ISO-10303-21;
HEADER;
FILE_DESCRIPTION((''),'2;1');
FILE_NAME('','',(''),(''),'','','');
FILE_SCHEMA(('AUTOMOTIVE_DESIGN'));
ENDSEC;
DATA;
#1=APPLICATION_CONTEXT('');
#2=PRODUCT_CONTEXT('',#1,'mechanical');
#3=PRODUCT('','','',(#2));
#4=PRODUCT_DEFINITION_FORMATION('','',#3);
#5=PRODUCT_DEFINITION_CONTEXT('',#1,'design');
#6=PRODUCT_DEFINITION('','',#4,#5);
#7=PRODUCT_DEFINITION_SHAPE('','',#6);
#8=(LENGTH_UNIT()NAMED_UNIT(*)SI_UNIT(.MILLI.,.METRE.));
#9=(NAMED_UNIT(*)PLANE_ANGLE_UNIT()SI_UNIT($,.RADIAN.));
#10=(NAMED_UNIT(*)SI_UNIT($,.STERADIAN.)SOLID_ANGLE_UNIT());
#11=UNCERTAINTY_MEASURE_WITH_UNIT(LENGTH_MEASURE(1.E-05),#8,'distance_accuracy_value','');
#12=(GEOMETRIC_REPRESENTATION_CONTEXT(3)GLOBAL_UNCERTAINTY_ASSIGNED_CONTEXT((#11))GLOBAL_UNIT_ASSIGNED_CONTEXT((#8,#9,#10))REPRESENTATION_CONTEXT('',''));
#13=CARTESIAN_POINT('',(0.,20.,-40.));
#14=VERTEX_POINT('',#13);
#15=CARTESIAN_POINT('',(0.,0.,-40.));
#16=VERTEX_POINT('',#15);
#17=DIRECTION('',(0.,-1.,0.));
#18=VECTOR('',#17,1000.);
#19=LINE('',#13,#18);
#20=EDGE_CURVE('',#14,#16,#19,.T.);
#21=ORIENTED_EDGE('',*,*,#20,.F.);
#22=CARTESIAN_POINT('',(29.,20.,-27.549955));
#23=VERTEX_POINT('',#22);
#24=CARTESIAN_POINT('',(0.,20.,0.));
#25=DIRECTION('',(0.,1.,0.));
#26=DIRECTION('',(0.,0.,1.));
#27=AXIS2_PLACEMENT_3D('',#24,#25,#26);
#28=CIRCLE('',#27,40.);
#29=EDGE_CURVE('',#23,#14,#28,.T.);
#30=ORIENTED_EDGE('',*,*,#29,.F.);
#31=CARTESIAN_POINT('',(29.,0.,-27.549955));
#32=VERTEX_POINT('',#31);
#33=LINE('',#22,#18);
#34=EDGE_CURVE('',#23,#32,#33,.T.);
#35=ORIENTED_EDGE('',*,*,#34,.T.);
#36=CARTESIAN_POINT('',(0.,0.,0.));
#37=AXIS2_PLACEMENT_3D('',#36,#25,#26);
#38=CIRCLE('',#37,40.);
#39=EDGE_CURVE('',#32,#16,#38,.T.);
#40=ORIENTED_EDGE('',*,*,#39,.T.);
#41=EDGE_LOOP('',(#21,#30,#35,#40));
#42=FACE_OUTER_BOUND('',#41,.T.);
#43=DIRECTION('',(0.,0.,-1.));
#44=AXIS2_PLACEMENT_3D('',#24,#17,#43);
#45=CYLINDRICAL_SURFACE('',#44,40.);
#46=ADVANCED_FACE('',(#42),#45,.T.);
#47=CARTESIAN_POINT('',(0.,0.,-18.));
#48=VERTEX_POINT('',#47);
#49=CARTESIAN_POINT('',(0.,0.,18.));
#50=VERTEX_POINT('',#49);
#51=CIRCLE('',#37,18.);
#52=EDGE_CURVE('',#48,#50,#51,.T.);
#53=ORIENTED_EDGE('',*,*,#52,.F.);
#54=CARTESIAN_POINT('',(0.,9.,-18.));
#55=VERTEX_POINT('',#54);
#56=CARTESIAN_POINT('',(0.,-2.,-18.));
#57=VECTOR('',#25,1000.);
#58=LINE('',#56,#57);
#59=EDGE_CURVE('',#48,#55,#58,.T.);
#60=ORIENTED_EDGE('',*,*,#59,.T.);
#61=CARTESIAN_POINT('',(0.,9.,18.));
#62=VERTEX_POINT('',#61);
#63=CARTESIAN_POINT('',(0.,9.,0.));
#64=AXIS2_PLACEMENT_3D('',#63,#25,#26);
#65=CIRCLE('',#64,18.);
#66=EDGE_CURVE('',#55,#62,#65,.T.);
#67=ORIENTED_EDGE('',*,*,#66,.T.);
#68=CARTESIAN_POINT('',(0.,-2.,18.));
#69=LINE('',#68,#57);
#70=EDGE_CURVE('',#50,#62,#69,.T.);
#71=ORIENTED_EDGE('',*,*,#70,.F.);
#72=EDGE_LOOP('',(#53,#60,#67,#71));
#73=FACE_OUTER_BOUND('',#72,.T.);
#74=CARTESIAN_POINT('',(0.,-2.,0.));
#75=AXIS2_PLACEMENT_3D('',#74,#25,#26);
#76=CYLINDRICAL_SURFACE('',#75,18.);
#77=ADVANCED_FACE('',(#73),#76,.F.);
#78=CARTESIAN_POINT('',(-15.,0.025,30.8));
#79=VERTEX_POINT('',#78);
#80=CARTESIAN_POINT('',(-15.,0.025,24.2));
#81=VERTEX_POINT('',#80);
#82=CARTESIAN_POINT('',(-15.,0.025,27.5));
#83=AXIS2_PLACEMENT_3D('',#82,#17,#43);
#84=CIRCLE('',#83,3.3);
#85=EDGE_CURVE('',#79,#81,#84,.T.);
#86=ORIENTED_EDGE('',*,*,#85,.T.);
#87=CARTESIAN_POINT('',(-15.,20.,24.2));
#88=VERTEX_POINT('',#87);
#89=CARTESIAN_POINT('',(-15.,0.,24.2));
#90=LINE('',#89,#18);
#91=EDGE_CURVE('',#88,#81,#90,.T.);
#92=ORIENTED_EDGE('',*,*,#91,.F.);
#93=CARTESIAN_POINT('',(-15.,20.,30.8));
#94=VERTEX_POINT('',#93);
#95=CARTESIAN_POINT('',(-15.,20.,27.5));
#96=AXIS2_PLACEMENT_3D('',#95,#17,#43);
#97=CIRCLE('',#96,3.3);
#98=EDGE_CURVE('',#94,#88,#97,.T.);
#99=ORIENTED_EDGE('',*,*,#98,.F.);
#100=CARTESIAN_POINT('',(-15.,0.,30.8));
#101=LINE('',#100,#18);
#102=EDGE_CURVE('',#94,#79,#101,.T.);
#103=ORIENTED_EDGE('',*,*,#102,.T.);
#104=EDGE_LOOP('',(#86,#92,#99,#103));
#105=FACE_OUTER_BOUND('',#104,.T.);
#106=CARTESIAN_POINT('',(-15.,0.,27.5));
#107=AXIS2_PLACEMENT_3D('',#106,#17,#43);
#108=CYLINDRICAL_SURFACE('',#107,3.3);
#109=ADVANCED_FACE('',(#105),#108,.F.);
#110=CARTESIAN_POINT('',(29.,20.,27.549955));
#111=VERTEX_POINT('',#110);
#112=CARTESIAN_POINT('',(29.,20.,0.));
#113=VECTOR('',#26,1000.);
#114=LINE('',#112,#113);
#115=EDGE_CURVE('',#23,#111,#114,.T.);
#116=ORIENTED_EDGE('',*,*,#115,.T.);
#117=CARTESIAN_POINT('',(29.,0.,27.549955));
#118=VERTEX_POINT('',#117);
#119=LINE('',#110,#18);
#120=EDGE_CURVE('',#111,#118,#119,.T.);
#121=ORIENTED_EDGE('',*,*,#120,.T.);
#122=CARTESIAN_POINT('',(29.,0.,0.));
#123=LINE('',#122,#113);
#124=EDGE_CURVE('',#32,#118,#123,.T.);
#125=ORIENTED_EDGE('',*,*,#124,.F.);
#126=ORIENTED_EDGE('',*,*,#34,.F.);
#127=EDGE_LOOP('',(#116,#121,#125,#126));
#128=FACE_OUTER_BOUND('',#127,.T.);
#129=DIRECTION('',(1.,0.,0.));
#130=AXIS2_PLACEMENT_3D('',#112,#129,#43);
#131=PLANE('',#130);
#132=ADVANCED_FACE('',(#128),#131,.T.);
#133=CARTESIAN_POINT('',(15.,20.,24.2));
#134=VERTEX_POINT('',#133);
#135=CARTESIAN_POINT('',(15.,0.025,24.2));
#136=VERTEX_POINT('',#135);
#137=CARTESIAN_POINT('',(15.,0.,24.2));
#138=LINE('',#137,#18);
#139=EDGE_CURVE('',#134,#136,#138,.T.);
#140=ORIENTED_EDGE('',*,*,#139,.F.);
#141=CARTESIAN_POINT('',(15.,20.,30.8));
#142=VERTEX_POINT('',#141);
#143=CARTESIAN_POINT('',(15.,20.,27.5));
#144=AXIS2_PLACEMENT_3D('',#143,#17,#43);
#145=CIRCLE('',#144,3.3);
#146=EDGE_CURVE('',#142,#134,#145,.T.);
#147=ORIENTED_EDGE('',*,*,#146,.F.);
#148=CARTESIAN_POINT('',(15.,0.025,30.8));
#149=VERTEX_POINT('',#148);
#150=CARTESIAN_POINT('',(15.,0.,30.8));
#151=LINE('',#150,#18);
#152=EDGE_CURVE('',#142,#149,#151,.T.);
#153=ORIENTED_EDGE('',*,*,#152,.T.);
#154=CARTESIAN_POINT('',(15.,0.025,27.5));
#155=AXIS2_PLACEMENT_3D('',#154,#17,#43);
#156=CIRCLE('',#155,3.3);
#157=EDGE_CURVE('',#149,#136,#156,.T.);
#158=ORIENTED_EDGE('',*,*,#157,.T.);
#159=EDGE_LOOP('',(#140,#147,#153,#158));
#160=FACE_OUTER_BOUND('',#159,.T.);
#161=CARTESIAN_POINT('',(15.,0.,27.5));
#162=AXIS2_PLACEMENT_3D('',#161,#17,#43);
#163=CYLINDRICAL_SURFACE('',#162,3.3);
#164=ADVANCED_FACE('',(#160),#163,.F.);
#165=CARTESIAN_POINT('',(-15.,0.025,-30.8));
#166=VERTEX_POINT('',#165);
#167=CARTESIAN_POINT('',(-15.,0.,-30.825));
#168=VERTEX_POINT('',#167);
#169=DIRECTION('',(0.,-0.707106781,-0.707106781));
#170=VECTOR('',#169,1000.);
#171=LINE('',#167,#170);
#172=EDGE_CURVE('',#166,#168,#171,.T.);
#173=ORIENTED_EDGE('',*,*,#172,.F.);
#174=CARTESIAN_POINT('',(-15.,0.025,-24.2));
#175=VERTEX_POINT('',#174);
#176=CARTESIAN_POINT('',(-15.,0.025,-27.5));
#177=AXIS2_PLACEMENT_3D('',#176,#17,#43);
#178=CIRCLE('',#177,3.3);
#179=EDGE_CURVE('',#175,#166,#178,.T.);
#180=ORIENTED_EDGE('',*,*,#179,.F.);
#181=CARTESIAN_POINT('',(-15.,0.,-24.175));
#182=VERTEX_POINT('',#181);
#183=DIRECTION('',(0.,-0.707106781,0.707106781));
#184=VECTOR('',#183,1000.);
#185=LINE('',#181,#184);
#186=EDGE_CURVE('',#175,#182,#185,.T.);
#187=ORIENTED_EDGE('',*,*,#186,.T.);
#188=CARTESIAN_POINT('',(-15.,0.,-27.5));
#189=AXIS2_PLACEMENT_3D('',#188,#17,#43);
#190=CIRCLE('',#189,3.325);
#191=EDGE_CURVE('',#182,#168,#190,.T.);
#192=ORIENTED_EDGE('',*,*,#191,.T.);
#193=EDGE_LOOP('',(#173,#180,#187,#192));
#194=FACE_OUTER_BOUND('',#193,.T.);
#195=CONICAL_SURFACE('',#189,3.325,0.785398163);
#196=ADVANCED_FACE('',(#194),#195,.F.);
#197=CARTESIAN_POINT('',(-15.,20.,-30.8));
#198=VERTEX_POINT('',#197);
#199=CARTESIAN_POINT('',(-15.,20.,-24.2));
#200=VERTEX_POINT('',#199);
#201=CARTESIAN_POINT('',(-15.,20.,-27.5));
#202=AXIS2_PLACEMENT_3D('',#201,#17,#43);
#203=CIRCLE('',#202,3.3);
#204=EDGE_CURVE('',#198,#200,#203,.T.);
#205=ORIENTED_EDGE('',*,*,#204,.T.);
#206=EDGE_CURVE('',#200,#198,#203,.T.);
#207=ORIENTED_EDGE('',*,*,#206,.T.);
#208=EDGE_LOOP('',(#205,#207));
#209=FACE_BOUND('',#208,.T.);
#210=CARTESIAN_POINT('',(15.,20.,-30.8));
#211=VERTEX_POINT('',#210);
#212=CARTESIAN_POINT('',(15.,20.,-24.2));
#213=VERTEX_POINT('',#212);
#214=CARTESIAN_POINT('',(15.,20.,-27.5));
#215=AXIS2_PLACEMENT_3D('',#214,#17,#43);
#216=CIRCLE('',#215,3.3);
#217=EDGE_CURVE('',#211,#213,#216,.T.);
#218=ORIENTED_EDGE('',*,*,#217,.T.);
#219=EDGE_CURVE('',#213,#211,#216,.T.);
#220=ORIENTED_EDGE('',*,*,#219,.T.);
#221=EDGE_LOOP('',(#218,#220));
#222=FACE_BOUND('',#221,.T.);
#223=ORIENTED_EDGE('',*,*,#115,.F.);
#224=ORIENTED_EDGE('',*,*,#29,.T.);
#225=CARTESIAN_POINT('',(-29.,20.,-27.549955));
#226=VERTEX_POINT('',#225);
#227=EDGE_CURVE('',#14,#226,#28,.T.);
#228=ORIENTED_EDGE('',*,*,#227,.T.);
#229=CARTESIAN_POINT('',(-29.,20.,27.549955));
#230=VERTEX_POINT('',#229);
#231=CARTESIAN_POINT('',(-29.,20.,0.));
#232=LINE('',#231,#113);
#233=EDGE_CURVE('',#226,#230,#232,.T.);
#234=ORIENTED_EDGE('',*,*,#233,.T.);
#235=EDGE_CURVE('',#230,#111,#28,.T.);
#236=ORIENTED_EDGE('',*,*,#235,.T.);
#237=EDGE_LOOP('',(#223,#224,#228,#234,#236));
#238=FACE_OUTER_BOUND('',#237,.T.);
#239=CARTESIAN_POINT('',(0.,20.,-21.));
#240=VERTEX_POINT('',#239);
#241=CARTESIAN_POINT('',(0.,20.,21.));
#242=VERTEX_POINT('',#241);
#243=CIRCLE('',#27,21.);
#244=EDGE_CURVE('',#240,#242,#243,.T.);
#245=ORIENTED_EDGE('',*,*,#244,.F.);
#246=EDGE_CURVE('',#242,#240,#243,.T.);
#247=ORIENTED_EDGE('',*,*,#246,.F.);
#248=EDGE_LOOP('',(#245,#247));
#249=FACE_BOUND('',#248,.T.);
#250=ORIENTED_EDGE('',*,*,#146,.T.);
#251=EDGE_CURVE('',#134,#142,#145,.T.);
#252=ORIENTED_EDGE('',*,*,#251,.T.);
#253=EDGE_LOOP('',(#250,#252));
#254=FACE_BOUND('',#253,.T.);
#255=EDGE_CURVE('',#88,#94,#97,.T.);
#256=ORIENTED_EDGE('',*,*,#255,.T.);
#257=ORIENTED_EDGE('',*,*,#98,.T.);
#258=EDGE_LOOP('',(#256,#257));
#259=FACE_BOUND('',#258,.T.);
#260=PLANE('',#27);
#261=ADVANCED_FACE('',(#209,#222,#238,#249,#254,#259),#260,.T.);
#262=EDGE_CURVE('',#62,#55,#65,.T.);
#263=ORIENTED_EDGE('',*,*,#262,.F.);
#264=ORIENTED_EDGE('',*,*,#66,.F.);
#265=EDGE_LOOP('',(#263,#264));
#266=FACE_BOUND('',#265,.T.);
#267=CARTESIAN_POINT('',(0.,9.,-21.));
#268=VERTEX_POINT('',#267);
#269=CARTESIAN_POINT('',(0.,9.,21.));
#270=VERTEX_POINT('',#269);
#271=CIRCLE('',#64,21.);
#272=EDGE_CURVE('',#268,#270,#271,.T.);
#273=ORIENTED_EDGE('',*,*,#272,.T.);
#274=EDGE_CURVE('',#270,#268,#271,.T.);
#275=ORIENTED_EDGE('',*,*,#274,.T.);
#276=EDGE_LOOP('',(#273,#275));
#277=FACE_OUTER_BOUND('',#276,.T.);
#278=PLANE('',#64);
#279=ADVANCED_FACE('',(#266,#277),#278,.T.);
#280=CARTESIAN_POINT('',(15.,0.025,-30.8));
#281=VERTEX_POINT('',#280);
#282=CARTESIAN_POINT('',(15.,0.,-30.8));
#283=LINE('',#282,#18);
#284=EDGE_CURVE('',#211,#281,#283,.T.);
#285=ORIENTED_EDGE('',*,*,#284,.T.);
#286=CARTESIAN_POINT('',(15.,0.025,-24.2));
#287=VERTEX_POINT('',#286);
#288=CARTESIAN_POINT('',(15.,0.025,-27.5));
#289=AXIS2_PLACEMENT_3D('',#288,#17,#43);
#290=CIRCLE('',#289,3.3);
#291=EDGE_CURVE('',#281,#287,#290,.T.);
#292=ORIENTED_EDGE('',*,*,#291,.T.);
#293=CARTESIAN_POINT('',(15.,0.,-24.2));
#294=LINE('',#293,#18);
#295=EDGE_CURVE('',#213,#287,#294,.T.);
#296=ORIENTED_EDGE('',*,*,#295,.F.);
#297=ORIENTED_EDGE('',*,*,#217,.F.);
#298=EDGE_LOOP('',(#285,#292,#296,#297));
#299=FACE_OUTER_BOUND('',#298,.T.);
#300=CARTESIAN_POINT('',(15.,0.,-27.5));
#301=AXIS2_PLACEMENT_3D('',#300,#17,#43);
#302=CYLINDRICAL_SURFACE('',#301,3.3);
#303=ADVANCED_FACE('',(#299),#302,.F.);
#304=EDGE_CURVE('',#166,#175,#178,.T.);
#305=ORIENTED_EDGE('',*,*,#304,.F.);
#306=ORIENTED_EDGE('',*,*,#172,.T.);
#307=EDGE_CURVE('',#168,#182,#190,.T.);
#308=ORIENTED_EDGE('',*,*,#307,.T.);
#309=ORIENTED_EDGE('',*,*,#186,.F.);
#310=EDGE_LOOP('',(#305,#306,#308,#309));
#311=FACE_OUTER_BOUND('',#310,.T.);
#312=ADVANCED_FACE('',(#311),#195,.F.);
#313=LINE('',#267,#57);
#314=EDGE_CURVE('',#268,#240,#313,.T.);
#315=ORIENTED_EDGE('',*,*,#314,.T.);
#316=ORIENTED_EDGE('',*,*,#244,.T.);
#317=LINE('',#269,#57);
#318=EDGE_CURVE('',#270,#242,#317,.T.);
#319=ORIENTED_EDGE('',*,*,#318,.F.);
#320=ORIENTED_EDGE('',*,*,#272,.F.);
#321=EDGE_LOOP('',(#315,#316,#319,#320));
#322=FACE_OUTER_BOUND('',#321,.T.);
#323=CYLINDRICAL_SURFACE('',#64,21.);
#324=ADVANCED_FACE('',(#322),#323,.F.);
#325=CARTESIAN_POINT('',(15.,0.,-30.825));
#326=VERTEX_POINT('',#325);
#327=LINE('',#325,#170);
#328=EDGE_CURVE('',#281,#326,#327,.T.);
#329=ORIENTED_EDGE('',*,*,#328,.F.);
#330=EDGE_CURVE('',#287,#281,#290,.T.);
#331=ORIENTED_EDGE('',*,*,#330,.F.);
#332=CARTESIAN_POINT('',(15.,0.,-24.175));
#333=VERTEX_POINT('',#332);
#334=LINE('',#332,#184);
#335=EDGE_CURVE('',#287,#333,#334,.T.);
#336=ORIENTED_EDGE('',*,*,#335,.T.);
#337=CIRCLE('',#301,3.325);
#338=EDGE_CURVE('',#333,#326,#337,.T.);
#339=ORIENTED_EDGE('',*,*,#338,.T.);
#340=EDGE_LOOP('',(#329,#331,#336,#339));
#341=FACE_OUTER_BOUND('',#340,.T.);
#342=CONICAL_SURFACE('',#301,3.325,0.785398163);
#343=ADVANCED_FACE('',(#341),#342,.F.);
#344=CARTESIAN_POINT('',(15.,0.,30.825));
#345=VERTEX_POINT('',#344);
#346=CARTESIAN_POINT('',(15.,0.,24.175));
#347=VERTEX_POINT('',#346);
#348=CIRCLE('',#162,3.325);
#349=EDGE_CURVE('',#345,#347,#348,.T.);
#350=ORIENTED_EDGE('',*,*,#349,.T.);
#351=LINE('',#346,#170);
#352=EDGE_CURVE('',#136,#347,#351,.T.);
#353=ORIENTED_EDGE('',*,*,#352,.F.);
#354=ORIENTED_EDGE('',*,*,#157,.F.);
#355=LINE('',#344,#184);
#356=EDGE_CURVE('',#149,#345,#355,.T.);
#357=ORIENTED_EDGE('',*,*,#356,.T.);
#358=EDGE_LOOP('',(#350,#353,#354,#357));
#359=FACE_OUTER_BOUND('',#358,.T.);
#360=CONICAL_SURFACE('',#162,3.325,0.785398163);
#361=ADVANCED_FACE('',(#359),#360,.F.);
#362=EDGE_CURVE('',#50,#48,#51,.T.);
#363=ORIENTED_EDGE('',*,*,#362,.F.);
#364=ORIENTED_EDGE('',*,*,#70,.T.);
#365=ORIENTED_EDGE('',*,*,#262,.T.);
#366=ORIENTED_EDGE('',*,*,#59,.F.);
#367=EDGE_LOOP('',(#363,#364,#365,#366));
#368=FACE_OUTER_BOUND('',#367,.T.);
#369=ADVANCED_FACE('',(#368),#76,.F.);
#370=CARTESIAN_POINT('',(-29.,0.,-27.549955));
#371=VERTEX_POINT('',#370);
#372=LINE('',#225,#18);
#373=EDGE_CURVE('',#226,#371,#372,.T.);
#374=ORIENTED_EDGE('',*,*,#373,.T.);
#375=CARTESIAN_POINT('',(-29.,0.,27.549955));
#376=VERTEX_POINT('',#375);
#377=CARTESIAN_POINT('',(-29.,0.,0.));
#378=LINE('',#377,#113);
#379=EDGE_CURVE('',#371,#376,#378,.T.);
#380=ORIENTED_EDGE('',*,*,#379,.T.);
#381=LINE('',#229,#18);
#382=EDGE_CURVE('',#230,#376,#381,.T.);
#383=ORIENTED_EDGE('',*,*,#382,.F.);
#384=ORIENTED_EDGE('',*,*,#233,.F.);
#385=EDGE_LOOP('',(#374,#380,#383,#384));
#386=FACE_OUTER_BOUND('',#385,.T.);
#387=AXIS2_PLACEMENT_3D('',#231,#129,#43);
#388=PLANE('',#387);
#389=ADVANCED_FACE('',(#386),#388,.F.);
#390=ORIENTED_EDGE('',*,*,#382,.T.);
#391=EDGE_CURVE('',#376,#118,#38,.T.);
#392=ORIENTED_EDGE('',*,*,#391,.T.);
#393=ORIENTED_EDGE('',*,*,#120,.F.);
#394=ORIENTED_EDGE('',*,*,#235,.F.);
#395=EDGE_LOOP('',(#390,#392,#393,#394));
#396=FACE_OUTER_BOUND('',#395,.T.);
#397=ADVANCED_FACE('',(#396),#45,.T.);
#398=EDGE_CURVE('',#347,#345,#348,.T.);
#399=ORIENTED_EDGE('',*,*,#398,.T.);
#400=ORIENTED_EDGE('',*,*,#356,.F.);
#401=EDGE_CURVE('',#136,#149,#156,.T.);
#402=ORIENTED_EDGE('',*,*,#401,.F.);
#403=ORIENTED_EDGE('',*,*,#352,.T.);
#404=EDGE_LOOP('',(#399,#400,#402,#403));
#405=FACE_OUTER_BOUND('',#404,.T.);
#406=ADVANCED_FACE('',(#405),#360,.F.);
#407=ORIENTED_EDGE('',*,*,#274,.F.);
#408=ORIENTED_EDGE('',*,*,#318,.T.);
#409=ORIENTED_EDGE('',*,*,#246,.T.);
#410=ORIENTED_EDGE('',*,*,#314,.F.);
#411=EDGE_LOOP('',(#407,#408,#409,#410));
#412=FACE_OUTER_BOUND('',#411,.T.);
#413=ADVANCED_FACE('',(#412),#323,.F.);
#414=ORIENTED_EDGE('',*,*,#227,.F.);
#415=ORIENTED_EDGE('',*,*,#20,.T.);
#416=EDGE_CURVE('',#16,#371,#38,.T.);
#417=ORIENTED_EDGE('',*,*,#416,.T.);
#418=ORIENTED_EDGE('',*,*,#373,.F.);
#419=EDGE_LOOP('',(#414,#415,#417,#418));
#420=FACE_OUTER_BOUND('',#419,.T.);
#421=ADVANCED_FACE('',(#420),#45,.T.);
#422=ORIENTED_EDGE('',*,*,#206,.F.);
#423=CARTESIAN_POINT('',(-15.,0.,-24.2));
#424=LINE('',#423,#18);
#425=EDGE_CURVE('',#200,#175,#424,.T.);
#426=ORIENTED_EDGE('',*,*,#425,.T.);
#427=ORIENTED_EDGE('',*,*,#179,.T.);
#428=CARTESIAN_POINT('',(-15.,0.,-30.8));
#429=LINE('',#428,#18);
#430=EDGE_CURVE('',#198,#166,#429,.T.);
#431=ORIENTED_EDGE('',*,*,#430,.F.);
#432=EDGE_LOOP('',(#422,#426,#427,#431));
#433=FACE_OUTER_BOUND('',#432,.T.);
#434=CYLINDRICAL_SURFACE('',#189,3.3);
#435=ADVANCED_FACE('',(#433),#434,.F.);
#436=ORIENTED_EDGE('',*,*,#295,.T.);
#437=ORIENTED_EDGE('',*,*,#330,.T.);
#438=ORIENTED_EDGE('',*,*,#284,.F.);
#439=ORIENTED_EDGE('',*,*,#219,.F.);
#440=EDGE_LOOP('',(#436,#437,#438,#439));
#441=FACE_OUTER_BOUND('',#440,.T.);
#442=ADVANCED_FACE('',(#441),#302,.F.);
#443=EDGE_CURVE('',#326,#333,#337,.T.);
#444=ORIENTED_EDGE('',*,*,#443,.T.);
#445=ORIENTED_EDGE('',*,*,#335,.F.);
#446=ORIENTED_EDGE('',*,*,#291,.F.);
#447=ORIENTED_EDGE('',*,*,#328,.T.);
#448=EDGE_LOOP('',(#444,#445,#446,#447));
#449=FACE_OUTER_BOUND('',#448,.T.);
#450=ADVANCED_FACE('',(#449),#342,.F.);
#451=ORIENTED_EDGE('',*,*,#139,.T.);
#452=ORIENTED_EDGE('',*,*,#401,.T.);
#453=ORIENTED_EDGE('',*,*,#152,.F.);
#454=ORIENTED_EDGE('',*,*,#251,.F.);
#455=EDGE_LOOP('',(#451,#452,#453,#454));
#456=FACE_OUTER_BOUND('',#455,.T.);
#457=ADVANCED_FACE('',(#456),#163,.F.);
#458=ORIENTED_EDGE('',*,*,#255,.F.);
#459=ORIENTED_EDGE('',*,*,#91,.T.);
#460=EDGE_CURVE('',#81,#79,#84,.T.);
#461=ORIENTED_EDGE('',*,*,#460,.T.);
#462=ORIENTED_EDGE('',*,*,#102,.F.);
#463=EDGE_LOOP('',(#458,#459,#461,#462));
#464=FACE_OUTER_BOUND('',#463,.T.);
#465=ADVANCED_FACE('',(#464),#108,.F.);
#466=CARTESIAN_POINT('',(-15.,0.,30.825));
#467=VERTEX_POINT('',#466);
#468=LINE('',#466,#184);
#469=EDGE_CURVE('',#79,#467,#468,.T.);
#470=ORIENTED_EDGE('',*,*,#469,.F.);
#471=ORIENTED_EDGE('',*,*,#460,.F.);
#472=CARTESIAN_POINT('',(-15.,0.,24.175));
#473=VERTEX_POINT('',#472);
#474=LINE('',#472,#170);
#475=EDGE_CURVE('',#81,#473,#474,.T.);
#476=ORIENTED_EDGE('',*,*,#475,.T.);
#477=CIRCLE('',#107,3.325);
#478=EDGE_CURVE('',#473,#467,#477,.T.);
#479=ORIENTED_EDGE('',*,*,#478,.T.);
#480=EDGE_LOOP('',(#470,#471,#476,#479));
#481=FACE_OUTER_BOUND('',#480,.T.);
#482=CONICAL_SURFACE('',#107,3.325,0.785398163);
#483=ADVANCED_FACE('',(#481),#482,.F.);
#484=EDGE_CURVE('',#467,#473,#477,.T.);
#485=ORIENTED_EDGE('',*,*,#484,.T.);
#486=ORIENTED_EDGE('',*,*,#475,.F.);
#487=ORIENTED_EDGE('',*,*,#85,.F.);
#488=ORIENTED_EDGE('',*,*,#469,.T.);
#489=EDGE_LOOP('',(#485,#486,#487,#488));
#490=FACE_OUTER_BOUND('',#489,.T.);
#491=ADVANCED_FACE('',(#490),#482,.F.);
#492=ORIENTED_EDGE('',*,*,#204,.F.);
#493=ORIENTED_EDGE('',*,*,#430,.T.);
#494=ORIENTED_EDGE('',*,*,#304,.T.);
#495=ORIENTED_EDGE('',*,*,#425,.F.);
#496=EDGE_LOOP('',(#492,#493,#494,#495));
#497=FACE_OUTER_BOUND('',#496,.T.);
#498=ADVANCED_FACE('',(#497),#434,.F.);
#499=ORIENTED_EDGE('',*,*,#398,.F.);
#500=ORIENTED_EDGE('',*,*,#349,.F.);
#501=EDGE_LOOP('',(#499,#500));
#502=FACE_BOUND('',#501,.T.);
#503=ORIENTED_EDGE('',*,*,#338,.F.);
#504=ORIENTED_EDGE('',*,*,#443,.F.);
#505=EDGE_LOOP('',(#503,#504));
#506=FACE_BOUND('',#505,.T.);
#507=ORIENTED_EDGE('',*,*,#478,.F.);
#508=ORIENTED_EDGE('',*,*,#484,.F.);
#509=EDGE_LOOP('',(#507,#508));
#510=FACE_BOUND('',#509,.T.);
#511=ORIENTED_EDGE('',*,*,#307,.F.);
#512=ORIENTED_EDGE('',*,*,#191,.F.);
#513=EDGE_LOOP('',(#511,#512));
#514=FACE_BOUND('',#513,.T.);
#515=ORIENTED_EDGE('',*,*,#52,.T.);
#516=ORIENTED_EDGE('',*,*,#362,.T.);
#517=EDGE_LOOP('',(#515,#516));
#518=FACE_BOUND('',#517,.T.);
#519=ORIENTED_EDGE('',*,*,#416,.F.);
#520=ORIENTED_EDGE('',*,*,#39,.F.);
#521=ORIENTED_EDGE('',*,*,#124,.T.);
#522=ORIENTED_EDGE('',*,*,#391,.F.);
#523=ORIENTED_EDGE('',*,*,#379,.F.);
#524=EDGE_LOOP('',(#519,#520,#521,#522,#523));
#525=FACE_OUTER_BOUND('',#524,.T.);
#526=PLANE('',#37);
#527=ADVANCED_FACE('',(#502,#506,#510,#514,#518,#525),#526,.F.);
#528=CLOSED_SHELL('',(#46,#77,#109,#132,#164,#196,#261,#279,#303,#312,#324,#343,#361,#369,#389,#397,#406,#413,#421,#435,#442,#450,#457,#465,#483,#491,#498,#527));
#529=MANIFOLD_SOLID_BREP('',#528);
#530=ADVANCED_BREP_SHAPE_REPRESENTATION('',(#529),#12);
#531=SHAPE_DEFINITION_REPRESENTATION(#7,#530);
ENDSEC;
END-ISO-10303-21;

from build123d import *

# Parameters (mm, degrees)
SKETCH1_R                      = 40
BOSS_EXTRUDE1_DEPTH            = 20
SKETCH2_R                      = 21
CUT_EXTRUDE1_DEPTH             = 11
SKETCH3_R                      = 18
CUT_EXTRUDE2_DEPTH             = 11
CUT_EXTRUDE3_DEPTH             = 61
M6_CLEARANCE_HOLE2_D           = 6.6
M6_CLEARANCE_HOLE2_CSINK_D     = 6.65
M6_CLEARANCE_HOLE2_CSINK_ANGLE = 90


with BuildPart() as part:
    # Sketch1 → Boss-Extrude1 (new body)
    with BuildSketch(Plane(origin=(0, 0, 0), x_dir=(1, 0, 0), z_dir=(0, 1, 0))):
        with Locations(Location((0, 0, 0), (0, 0, 270))):
            Circle(SKETCH1_R)
    extrude(amount=BOSS_EXTRUDE1_DEPTH)

    # Sketch2 → Cut-Extrude1 (cut)
    with BuildSketch(Plane(origin=(0, 20, 0), x_dir=(1, 0, 0), z_dir=(0, 1, 0))):
        with Locations(Location((0, 0, 0), (0, 0, 270))):
            Circle(SKETCH2_R)
    extrude(amount=-CUT_EXTRUDE1_DEPTH, mode=Mode.SUBTRACT)

    # Sketch3 → Cut-Extrude2 (cut)
    with BuildSketch(Plane(origin=(0, 9, 0), x_dir=(1, 0, 0), z_dir=(0, 1, 0))):
        with Locations(Location((0, 0, 0), (0, 0, 270))):
            Circle(SKETCH3_R)
    extrude(amount=-CUT_EXTRUDE2_DEPTH, mode=Mode.SUBTRACT)

    # Sketch8 → Cut-Extrude3 (cut, through all)
    with BuildSketch(Plane.XZ):
        with BuildLine():
            ThreePointArc((40, 0), (37.148351242, 14.832396974), (29, 27.549954628))
            Line((29, 27.549954628), (29, -27.549954628))
            ThreePointArc((29, -27.549954628), (37.148351242, -14.832396974), (40, 0))
        make_face()
        with BuildLine():
            ThreePointArc((-29, 27.549954628), (-40, 0), (-29, -27.549954628))
            Line((-29, -27.549954628), (-29, 27.549954628))
        make_face()
    extrude(amount=-CUT_EXTRUDE3_DEPTH, mode=Mode.SUBTRACT)

    # M6 Clearance Hole2 (through all)
    with Locations(Plane(origin=(0, 0, 0), x_dir=(-1, 0, 0), z_dir=(0, -1, 0))):
        with Locations((-15, -27.5), (15, -27.5), (15, 27.5), (-15, 27.5)):
            CounterSinkHole(M6_CLEARANCE_HOLE2_D / 2, M6_CLEARANCE_HOLE2_CSINK_D / 2, counter_sink_angle=M6_CLEARANCE_HOLE2_CSINK_ANGLE)


solid = part.part
